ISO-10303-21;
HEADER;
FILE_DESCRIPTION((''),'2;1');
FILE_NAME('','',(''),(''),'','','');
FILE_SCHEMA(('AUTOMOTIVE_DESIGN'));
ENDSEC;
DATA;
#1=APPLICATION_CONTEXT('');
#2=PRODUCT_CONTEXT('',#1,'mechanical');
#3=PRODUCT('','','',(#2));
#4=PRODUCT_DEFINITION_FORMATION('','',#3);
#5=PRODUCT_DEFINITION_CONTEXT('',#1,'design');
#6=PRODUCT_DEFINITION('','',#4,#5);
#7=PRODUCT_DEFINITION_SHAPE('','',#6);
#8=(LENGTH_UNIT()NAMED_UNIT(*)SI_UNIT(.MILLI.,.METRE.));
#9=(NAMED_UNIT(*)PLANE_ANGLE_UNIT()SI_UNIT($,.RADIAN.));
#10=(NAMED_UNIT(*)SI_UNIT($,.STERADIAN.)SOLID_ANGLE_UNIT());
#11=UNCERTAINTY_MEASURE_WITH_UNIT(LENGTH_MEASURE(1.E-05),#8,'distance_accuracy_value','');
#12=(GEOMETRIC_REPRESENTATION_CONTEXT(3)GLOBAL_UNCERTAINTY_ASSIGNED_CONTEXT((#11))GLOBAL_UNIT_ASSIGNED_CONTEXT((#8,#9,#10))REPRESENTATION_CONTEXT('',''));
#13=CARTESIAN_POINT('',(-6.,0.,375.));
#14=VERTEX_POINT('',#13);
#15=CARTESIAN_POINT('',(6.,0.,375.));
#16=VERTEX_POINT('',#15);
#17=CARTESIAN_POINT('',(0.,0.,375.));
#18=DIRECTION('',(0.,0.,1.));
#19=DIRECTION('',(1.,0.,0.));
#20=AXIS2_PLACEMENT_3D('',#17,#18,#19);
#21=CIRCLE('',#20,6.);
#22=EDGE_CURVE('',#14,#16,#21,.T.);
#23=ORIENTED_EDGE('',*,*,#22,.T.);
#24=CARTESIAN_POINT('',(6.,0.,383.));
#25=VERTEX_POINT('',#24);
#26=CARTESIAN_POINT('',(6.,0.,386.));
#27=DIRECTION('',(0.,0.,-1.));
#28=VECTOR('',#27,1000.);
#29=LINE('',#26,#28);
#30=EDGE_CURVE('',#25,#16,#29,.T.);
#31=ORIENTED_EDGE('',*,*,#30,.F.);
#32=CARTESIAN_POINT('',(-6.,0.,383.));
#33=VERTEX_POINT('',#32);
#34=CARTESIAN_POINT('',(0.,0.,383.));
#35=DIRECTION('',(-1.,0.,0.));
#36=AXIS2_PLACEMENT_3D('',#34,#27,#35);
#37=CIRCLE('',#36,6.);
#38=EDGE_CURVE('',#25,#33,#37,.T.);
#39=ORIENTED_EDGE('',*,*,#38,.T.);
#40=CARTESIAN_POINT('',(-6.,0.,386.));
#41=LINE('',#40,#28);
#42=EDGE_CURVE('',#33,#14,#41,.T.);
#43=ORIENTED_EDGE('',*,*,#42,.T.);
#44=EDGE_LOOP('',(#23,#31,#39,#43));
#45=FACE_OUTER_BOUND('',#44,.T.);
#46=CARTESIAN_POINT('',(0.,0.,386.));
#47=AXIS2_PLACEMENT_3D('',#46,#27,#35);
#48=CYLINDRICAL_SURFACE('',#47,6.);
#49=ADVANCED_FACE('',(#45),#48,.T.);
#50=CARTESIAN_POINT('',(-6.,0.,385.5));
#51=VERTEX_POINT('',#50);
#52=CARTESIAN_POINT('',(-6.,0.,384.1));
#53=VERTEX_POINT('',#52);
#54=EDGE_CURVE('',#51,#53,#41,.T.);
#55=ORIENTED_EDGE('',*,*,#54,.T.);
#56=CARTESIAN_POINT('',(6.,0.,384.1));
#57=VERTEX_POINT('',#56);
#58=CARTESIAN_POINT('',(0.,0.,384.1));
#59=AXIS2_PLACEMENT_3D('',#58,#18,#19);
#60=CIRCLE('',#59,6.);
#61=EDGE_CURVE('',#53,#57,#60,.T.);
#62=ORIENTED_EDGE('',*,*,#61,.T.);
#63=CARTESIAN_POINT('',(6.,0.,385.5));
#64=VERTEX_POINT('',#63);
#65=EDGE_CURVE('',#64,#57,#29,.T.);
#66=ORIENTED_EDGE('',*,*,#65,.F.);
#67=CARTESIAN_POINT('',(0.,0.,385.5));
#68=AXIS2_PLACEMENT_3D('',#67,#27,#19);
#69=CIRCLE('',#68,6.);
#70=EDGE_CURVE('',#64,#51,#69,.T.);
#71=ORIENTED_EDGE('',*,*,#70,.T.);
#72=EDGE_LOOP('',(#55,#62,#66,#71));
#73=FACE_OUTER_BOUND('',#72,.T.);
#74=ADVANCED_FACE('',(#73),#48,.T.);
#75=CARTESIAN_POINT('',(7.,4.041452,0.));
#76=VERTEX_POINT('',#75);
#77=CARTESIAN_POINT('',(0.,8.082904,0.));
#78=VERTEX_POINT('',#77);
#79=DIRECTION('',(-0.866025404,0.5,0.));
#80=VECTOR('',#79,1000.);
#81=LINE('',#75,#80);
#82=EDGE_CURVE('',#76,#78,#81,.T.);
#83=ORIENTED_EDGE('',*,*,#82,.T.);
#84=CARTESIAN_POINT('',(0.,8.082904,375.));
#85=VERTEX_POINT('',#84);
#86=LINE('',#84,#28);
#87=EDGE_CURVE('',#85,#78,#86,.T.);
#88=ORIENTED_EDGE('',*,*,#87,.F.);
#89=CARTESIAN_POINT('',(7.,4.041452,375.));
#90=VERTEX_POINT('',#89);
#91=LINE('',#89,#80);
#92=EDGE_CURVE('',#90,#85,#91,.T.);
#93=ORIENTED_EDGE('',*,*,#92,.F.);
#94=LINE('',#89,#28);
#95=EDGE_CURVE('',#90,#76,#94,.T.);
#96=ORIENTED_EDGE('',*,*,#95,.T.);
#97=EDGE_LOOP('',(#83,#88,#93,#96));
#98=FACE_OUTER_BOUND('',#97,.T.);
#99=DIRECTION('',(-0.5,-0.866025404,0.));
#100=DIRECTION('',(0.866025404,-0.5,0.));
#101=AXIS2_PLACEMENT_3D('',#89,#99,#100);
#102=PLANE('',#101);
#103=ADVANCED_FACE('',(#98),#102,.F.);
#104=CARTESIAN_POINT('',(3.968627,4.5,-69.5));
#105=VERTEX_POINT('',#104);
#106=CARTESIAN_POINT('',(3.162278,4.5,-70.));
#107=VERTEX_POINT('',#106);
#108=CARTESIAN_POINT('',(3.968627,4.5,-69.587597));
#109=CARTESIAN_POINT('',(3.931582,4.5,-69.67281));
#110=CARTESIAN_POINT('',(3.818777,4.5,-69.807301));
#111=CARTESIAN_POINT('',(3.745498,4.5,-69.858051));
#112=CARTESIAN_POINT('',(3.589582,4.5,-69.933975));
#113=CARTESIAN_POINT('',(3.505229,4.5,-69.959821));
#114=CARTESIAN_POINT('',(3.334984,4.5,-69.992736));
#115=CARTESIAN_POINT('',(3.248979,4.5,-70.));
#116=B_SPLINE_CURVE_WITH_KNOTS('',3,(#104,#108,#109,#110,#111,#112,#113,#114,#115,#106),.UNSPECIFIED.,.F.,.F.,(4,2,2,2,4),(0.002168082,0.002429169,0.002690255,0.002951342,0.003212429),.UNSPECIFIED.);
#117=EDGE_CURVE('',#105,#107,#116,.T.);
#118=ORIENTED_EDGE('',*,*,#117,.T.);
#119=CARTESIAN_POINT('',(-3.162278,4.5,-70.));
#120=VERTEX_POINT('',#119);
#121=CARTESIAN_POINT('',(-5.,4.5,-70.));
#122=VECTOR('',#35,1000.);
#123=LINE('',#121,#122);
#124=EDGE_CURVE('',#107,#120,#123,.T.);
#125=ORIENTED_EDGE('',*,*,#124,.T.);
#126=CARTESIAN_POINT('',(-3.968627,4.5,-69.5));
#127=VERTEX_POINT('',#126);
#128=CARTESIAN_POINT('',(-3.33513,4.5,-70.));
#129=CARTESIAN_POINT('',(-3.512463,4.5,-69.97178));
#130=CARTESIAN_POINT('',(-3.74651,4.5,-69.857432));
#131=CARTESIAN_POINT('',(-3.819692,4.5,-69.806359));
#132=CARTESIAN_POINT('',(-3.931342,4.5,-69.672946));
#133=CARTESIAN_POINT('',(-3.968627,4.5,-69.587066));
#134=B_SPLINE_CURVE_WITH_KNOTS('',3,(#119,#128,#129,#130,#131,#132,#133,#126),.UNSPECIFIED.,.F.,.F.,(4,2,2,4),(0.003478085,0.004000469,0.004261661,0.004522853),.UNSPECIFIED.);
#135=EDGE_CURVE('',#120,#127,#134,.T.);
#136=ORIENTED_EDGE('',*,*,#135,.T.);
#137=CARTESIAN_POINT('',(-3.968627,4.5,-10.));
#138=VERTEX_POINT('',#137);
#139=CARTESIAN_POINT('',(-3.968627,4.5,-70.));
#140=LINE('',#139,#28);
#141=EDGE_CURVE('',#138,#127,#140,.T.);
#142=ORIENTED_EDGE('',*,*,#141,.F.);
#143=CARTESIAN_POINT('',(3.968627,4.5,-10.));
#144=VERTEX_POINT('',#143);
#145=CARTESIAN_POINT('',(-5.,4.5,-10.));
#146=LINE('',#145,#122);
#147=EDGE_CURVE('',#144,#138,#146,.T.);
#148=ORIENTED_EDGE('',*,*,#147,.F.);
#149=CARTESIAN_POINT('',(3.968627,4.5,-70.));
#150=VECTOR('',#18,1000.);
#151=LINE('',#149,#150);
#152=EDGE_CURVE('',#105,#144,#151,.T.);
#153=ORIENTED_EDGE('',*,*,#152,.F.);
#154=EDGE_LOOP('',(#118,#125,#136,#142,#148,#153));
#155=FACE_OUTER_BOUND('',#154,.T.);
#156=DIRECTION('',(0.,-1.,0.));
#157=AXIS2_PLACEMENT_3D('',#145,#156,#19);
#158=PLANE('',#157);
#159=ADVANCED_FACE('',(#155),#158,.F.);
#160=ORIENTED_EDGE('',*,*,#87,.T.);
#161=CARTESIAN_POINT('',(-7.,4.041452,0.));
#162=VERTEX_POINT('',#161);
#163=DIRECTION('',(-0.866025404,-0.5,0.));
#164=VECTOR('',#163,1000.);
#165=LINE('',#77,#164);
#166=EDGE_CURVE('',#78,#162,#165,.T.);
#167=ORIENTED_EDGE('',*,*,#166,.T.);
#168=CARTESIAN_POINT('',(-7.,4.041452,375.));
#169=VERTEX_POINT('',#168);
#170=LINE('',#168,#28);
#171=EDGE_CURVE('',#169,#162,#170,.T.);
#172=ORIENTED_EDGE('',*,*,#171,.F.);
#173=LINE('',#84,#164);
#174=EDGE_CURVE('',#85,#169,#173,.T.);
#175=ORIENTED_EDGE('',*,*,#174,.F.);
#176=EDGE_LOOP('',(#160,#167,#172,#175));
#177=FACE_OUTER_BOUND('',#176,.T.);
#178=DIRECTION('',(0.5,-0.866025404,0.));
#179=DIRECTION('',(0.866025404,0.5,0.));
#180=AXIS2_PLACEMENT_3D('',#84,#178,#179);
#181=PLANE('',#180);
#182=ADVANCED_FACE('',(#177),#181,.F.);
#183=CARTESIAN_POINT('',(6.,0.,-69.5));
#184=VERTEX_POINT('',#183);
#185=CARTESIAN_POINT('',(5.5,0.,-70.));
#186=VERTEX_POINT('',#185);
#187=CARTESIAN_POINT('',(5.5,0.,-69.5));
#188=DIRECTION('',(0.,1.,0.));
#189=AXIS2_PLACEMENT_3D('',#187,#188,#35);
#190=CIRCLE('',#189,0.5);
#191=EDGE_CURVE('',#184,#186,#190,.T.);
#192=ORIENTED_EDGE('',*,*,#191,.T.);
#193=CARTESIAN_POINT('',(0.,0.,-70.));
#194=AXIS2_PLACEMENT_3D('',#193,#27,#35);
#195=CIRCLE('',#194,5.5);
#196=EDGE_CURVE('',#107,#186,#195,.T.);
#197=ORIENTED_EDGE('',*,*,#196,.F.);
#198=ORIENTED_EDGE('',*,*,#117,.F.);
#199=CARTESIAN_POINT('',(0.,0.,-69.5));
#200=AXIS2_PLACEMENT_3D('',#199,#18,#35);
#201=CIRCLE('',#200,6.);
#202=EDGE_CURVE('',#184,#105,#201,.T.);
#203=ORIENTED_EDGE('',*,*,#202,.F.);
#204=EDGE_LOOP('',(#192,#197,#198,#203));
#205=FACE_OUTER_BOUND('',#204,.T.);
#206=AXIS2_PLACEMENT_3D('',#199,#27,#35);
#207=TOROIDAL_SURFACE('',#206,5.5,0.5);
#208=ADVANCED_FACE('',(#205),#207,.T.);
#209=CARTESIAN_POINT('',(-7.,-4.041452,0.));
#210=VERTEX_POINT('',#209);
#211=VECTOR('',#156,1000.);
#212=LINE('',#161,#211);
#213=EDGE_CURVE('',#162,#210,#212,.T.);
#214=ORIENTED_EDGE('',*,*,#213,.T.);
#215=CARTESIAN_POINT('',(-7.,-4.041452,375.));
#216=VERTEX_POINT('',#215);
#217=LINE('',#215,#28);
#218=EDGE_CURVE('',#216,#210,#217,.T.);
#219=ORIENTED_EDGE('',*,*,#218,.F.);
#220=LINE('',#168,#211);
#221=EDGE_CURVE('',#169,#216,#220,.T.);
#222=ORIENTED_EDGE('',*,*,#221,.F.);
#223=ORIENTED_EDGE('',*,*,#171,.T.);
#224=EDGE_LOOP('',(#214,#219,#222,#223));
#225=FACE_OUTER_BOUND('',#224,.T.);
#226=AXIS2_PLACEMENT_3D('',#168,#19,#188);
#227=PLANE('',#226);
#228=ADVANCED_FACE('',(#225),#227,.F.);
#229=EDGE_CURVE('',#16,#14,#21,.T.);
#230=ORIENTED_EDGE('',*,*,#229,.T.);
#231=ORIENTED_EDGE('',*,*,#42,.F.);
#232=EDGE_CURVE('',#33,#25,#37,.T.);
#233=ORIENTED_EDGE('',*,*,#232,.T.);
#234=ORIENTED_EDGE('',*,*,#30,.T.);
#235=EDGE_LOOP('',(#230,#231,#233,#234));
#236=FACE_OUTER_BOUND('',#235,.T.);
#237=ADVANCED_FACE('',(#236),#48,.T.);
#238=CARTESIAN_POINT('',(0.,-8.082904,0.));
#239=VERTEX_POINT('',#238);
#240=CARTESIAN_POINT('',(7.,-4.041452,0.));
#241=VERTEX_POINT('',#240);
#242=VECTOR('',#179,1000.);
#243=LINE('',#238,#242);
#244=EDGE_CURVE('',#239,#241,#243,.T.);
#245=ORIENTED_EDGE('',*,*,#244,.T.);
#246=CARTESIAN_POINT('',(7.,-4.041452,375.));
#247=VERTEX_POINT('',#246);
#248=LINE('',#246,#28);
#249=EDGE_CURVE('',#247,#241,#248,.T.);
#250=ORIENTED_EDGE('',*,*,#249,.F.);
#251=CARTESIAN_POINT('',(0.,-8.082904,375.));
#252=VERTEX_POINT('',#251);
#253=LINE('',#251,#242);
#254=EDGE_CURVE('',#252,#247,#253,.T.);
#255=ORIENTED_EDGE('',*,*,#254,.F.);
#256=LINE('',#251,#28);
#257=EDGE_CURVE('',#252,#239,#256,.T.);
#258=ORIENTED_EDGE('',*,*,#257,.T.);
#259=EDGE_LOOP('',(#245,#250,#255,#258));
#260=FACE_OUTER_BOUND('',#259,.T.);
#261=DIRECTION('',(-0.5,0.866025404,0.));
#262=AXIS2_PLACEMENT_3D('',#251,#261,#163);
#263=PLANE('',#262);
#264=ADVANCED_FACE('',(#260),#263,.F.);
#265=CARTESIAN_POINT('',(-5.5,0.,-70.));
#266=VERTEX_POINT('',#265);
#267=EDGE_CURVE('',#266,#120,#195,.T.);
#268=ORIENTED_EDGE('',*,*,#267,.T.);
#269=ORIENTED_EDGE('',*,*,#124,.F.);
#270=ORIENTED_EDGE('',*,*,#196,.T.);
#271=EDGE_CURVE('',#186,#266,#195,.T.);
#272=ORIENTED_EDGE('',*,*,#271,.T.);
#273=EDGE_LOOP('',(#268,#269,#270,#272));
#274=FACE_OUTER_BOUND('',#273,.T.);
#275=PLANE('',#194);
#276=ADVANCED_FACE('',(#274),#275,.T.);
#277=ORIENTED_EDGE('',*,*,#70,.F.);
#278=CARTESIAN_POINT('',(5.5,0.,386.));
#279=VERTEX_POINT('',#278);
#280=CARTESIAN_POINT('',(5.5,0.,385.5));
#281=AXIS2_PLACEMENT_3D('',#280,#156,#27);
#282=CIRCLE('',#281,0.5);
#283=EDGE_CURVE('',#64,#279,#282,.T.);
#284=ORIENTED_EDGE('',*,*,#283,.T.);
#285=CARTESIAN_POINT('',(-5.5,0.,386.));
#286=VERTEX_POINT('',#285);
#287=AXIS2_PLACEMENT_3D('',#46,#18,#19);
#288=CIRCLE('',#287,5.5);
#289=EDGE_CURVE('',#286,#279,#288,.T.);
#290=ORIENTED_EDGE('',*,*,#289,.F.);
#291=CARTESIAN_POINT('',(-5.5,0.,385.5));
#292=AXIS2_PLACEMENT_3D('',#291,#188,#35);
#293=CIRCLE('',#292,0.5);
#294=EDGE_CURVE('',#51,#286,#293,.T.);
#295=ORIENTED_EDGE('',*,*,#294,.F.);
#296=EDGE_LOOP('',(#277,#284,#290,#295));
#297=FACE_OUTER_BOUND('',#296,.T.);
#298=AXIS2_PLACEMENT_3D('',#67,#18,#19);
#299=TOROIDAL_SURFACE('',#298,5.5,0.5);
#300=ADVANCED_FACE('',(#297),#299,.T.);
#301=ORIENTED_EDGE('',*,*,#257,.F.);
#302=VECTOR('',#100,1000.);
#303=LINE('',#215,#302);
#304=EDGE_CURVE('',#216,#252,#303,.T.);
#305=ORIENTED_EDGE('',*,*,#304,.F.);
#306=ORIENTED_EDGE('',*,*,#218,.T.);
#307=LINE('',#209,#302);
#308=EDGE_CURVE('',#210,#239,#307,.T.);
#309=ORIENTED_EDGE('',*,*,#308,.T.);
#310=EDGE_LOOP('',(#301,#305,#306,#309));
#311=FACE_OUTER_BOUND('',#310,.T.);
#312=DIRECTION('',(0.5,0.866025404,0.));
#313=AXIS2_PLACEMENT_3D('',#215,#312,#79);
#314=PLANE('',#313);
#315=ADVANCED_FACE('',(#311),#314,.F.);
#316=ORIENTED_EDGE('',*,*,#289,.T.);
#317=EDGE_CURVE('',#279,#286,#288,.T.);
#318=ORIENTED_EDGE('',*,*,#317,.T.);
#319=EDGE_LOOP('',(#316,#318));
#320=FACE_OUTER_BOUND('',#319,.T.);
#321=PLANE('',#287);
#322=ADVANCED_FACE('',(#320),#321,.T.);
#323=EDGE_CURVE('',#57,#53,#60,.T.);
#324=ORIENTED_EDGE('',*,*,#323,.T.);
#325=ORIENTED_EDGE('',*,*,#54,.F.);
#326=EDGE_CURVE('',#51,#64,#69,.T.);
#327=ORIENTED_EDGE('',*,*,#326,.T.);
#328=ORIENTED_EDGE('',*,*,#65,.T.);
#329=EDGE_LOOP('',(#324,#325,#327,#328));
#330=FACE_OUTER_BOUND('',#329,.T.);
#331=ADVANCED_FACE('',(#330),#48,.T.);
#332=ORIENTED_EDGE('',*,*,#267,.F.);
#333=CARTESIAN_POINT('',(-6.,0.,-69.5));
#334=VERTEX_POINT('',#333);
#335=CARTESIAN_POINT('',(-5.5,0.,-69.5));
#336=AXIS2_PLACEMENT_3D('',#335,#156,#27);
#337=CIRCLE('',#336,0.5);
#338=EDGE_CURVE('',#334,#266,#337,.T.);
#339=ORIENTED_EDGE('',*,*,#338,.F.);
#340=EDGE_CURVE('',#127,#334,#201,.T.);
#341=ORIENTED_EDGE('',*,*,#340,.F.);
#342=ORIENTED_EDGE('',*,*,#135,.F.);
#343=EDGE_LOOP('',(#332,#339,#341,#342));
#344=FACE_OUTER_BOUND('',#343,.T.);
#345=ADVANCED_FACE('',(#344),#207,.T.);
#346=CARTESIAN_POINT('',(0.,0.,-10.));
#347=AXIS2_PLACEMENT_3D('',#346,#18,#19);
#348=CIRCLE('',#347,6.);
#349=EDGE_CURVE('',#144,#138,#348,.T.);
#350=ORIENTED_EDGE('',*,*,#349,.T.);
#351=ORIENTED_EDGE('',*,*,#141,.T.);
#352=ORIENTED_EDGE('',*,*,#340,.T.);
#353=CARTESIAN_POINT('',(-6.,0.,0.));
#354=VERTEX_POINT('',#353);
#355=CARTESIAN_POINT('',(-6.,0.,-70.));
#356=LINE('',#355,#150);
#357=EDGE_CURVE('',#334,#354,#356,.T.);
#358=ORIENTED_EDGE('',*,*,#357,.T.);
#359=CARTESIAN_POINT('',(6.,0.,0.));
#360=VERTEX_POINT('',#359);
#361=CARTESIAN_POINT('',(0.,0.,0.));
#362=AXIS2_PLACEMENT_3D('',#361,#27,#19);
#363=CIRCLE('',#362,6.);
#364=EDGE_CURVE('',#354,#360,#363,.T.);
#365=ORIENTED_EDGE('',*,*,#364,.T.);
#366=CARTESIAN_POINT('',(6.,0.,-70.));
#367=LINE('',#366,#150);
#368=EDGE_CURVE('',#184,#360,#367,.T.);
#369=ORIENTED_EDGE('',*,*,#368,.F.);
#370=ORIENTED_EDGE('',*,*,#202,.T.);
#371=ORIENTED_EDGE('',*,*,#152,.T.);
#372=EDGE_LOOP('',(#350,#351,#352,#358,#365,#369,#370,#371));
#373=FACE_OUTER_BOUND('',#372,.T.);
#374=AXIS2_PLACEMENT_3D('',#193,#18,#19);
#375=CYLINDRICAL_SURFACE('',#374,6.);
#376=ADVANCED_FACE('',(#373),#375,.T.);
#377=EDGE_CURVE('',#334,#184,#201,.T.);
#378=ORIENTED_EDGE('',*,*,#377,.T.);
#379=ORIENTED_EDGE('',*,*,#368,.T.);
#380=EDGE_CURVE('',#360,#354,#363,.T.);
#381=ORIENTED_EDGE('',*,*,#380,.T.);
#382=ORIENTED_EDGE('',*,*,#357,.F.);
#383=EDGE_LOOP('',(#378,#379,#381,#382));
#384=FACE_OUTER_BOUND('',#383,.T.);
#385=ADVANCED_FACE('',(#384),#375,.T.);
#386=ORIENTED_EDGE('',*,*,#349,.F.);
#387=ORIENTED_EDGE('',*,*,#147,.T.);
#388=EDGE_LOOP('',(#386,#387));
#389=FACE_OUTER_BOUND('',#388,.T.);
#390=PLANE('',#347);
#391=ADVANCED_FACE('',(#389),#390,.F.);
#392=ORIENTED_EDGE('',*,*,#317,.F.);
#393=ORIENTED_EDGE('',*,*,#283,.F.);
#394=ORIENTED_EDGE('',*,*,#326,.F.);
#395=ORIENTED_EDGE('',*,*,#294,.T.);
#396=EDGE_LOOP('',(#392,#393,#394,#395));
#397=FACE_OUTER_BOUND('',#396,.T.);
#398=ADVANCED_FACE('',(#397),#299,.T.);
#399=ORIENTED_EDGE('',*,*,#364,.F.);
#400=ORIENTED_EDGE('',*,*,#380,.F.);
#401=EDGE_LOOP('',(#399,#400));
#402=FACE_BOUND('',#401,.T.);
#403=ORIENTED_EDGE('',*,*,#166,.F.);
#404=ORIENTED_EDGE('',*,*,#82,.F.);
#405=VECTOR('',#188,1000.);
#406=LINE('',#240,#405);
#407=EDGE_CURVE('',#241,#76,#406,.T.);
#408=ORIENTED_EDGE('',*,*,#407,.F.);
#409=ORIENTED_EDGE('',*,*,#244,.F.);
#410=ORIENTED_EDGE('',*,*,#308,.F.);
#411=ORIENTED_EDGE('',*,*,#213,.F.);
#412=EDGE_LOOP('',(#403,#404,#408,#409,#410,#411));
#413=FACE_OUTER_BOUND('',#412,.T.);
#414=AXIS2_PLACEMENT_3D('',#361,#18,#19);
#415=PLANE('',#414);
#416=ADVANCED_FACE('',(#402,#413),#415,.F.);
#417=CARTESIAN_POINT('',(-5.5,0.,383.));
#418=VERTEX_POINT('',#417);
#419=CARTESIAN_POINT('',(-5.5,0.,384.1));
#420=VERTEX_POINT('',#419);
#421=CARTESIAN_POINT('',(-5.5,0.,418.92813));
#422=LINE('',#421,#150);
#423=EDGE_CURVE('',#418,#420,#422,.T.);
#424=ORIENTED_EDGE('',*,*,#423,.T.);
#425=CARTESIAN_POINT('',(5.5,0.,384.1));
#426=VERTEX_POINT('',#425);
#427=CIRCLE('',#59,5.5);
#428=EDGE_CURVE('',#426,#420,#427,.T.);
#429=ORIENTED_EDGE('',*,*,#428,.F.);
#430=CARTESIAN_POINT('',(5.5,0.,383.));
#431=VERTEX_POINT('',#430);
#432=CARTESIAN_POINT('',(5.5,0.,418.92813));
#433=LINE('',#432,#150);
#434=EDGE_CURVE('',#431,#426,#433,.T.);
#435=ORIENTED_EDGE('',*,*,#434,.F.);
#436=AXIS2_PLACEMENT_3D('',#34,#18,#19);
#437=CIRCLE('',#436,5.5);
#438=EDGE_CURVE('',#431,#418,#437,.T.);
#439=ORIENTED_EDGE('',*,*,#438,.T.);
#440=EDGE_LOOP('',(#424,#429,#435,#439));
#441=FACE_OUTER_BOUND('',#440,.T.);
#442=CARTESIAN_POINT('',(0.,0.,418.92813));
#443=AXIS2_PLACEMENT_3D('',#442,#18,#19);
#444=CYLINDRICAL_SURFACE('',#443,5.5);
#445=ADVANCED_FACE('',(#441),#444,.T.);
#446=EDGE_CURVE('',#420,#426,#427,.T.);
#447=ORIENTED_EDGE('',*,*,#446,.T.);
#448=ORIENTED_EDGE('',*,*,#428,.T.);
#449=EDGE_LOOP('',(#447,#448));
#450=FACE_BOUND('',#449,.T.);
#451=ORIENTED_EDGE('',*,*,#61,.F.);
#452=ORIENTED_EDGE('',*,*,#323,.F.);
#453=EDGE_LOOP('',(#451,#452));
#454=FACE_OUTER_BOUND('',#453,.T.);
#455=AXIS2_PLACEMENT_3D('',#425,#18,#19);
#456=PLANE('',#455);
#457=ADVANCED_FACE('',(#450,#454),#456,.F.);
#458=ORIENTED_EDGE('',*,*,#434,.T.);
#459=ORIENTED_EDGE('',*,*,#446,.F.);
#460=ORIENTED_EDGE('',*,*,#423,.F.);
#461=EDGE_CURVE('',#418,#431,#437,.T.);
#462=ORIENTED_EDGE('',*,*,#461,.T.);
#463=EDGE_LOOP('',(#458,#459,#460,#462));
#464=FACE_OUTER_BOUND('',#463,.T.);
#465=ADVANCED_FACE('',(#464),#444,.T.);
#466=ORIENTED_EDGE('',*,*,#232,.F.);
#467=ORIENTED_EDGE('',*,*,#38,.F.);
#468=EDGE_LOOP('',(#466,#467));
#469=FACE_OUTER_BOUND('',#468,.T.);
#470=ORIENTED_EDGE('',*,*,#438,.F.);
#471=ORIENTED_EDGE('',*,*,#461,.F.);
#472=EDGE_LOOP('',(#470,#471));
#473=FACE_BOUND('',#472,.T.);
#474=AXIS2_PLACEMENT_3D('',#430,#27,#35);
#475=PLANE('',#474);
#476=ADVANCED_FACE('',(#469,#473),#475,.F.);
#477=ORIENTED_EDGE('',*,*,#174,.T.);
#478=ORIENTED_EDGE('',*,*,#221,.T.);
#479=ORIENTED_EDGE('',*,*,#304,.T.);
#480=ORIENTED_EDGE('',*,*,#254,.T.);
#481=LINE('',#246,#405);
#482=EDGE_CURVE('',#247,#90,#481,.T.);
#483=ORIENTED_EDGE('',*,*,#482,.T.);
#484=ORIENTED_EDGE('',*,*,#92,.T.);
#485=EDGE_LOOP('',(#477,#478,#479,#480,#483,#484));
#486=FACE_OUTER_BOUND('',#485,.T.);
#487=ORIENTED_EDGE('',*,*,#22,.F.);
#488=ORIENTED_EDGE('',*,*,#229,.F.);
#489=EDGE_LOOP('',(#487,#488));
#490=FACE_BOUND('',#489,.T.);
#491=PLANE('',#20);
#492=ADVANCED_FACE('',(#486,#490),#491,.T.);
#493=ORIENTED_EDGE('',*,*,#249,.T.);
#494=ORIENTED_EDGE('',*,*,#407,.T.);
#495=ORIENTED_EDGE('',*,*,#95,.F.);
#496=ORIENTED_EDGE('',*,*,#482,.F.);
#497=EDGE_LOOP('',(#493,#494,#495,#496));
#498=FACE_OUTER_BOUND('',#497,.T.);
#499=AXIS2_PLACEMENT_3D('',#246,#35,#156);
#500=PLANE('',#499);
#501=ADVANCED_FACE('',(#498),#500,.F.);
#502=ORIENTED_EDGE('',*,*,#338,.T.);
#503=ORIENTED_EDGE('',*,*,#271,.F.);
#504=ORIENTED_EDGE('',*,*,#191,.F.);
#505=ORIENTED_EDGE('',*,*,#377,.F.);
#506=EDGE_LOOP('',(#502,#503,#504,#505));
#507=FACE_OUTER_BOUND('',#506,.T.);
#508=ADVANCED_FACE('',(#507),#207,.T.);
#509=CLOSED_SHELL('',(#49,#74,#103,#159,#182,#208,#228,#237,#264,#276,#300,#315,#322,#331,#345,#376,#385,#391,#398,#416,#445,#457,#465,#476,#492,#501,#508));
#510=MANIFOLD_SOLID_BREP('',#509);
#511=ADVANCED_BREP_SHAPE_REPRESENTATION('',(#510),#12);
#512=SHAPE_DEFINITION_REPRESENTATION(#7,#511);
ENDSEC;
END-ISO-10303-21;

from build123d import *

# Parameters (mm, degrees)
EXTRUDE_1_DEPTH     = 375
SKETCH_2_R          = 6
EXTRUDE_2_DEPTH     = 70
EXTRUDE_START       = 11
SKETCH_3_R          = 6
EXTRUDE_3_DEPTH     = 11
FILLET_1_R          = 0.5
SKETCH_6_W          = 1
SKETCH_6_H          = 1.1
FILLET_2_R          = 0.5
SKETCH_7_W          = 10
SKETCH_7_H          = 2
CUT_EXTRUDE_1_DEPTH = 60


with BuildPart() as part:
    # 草图1 → 凸台-拉伸1 (new body)
    with BuildSketch(Plane.XY):
        Polygon((7, -4.041451884), (7, 4.041451884), (0, 8.082903769), (-7, 4.041451884), (-7, -4.041451884), (0, -8.082903769), align=None)
    extrude(amount=EXTRUDE_1_DEPTH)

    # 草图2 → 凸台-拉伸2 (add)
    with BuildSketch(Plane(origin=(0, 0, 0), x_dir=(-1, 0, 0), z_dir=(0, 0, -1))):
        with Locations(Location((0, 0, 0), (0, 0, 180))):
            Circle(SKETCH_2_R)
    extrude(amount=EXTRUDE_2_DEPTH)

    # 草图3 → 凸台-拉伸3 (add)
    with BuildSketch(Plane.XY.offset(375).offset(EXTRUDE_START)):
        Circle(SKETCH_3_R)
    extrude(amount=-EXTRUDE_3_DEPTH)

    # 圆角1
    fillet_1_edges = [part.edges().sort_by_distance(p)[0] for p in [
        (-6, 0, -70),
    ]]
    fillet(fillet_1_edges, radius=FILLET_1_R)

    # 草图6 → 切除-旋转2 (revolve, cut)
    with BuildSketch(Plane(origin=(0, 0, 0), x_dir=(1, 0, 0), z_dir=(0, 1, 0)), mode=Mode.PRIVATE) as cut_revolve_2_sk:
        with Locations((6, -383.55)):
            Rectangle(SKETCH_6_W, SKETCH_6_H)
    revolve(cut_revolve_2_sk.sketch.rotate(Axis((0, 0, 418.9281299), (0, 0, -1)), 180), axis=Axis((0, 0, 418.9281299), (0, 0, -1)), mode=Mode.SUBTRACT)

    # 圆角2
    fillet_2_edges = [part.edges().sort_by_distance(p)[0] for p in [
        (-6, 0, 386),
    ]]
    fillet(fillet_2_edges, radius=FILLET_2_R)

    # 草图7 → 切除-拉伸1 (cut)
    with BuildSketch(Plane(origin=(0, 0, -70), x_dir=(-1, 0, 0), z_dir=(0, 0, -1))):
        with Locations((0, 5.5)):
            Rectangle(SKETCH_7_W, SKETCH_7_H)
    extrude(amount=-CUT_EXTRUDE_1_DEPTH, mode=Mode.SUBTRACT)


solid = part.part
